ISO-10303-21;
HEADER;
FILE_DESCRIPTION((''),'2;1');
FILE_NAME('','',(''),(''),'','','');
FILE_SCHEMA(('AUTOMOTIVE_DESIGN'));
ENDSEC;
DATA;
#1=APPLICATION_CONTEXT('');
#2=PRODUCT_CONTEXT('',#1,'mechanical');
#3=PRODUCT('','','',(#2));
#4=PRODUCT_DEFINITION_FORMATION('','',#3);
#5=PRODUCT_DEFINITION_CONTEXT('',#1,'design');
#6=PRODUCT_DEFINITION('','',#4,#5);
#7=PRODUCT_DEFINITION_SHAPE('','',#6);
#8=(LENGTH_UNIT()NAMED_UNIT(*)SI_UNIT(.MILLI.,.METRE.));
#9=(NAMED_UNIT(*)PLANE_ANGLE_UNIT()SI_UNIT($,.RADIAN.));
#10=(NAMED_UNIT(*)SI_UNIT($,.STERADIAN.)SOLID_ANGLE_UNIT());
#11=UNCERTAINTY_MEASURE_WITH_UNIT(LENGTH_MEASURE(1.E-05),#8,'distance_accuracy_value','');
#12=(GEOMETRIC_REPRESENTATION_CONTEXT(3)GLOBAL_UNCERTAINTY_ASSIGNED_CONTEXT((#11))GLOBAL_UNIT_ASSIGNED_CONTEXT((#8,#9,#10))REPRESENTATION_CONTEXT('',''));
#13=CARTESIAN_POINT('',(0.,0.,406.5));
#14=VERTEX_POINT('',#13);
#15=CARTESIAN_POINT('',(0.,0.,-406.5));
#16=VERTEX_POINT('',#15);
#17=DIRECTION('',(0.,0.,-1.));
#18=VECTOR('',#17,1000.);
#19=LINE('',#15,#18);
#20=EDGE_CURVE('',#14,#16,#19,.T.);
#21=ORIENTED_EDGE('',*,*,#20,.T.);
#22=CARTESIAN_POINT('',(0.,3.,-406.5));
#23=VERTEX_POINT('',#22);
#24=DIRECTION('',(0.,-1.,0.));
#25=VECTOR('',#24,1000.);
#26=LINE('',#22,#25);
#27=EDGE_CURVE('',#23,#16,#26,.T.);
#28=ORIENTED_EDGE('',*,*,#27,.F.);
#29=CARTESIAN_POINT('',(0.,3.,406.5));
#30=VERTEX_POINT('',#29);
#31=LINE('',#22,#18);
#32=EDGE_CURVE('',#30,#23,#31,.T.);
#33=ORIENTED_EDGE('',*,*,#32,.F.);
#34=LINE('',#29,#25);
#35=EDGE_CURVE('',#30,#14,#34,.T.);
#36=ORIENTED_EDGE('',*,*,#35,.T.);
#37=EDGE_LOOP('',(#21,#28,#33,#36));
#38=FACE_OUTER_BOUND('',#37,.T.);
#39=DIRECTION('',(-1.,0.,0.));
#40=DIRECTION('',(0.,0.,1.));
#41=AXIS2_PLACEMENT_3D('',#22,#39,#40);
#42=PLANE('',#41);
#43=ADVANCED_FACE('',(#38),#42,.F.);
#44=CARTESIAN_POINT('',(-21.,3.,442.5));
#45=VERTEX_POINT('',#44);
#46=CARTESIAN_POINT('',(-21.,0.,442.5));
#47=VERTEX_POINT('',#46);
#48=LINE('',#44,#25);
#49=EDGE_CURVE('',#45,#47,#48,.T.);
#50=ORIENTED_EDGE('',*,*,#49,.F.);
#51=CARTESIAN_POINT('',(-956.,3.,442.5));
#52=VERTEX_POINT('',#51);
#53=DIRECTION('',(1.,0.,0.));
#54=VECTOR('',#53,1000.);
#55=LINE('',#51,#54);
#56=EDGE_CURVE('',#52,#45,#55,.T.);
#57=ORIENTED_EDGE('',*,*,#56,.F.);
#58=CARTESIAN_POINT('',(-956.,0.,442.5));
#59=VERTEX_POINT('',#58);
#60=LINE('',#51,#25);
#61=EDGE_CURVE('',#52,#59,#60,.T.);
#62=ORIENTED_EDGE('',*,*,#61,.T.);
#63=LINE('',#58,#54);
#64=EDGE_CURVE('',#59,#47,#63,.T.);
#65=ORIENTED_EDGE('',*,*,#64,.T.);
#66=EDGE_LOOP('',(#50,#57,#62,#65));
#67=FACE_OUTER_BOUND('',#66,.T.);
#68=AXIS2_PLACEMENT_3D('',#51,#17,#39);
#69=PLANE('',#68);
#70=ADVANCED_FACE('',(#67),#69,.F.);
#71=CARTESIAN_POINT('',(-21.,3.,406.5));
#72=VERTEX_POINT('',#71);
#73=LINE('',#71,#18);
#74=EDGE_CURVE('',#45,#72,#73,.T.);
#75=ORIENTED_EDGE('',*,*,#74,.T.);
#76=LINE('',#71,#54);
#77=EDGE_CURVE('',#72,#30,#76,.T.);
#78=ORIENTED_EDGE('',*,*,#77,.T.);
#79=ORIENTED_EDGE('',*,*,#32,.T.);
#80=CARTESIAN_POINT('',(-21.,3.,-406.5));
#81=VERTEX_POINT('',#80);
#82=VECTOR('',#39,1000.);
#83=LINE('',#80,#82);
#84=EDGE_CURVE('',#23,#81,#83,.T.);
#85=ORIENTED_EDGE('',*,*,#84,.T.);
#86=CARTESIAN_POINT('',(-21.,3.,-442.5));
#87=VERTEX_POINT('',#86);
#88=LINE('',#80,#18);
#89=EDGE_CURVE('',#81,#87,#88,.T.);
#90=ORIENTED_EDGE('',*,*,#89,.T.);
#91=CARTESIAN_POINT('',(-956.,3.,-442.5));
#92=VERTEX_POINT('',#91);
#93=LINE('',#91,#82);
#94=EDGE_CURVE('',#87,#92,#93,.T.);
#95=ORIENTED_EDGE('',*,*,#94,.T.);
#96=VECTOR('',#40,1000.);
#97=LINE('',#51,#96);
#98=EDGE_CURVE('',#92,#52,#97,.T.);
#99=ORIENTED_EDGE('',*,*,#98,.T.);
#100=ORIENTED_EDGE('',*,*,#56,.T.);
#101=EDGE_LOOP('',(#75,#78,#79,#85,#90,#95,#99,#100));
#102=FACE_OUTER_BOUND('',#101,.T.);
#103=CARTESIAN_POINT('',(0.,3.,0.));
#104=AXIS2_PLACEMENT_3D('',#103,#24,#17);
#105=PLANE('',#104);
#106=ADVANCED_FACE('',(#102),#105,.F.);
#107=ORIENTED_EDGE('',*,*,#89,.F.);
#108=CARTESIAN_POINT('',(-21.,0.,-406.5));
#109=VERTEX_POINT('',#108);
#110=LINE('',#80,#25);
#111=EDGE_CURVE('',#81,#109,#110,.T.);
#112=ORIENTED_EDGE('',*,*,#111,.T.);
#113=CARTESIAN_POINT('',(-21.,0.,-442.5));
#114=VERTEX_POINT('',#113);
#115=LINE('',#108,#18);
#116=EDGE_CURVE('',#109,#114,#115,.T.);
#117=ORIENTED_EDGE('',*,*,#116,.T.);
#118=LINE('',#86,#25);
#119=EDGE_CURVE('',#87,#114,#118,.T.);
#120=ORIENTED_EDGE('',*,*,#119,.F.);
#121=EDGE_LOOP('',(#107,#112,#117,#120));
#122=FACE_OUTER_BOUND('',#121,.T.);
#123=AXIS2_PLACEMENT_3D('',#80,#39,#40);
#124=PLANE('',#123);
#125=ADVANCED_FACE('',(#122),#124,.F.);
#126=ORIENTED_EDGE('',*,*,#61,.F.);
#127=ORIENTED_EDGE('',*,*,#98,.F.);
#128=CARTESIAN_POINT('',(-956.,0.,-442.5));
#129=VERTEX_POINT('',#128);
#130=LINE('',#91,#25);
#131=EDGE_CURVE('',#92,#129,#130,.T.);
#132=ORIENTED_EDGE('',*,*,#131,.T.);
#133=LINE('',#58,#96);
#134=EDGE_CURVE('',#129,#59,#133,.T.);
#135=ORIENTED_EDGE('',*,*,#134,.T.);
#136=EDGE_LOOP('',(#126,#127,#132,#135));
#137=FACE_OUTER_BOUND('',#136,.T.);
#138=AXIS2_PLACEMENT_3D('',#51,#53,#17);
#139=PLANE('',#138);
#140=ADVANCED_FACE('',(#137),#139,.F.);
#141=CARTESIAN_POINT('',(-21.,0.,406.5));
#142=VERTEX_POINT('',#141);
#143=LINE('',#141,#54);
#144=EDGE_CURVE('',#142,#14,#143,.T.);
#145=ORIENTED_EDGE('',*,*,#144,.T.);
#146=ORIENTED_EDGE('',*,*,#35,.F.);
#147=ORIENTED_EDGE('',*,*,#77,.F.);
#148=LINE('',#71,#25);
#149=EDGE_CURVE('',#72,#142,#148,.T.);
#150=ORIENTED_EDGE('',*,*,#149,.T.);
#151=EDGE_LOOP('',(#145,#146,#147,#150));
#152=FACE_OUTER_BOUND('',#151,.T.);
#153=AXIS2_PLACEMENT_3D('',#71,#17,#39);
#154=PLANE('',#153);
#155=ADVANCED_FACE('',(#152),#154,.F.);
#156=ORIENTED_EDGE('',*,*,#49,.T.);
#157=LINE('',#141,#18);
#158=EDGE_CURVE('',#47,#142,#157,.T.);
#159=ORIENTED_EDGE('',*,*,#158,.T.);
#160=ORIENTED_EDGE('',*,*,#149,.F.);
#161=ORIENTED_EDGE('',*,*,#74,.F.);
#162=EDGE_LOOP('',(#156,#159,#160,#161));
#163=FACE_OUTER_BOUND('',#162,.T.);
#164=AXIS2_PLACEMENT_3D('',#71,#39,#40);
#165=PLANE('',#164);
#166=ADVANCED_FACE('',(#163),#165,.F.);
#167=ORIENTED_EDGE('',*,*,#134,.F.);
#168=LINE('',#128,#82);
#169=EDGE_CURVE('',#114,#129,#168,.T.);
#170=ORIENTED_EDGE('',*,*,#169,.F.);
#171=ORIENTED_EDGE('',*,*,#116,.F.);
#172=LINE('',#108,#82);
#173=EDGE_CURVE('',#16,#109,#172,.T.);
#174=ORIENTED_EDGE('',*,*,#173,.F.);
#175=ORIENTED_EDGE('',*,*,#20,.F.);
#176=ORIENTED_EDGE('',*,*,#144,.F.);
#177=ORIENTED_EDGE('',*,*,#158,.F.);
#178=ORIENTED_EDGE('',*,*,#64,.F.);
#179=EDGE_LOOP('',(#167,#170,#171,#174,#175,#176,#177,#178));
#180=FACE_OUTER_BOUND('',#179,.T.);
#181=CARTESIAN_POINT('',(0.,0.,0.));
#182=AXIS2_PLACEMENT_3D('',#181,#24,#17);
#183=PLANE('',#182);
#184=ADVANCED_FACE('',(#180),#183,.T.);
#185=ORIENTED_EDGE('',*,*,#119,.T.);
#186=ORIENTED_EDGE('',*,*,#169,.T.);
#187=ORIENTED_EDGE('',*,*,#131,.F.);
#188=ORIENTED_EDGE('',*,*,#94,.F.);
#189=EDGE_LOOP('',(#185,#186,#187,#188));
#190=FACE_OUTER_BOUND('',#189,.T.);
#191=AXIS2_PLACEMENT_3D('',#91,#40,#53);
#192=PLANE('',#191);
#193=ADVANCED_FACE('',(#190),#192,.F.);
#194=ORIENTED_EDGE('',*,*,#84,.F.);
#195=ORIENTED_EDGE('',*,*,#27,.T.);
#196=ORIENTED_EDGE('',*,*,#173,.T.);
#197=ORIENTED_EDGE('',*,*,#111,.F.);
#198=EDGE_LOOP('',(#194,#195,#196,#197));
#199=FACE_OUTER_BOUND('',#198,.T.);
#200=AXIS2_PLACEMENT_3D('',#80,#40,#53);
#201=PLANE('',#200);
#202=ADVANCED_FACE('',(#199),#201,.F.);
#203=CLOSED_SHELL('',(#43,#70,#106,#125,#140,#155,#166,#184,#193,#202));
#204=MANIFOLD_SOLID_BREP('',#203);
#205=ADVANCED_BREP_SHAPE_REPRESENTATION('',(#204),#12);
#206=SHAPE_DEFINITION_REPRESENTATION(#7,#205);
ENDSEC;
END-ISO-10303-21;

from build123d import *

# Parameters (mm, degrees)
BOSS_EXTRUDE1_DEPTH = 3


with BuildPart() as part:
    # Sketch1 → Boss-Extrude1 (new body)
    with BuildSketch(Plane(origin=(0, 0, 0), x_dir=(1, 0, 0), z_dir=(0, 1, 0))):
        Polygon((-21, -406.5), (0, -406.5), (0, 406.5), (-21, 406.5), (-21, 442.5), (-956, 442.5), (-956, -442.5), (-21, -442.5), align=None)
    extrude(amount=BOSS_EXTRUDE1_DEPTH)


solid = part.part
